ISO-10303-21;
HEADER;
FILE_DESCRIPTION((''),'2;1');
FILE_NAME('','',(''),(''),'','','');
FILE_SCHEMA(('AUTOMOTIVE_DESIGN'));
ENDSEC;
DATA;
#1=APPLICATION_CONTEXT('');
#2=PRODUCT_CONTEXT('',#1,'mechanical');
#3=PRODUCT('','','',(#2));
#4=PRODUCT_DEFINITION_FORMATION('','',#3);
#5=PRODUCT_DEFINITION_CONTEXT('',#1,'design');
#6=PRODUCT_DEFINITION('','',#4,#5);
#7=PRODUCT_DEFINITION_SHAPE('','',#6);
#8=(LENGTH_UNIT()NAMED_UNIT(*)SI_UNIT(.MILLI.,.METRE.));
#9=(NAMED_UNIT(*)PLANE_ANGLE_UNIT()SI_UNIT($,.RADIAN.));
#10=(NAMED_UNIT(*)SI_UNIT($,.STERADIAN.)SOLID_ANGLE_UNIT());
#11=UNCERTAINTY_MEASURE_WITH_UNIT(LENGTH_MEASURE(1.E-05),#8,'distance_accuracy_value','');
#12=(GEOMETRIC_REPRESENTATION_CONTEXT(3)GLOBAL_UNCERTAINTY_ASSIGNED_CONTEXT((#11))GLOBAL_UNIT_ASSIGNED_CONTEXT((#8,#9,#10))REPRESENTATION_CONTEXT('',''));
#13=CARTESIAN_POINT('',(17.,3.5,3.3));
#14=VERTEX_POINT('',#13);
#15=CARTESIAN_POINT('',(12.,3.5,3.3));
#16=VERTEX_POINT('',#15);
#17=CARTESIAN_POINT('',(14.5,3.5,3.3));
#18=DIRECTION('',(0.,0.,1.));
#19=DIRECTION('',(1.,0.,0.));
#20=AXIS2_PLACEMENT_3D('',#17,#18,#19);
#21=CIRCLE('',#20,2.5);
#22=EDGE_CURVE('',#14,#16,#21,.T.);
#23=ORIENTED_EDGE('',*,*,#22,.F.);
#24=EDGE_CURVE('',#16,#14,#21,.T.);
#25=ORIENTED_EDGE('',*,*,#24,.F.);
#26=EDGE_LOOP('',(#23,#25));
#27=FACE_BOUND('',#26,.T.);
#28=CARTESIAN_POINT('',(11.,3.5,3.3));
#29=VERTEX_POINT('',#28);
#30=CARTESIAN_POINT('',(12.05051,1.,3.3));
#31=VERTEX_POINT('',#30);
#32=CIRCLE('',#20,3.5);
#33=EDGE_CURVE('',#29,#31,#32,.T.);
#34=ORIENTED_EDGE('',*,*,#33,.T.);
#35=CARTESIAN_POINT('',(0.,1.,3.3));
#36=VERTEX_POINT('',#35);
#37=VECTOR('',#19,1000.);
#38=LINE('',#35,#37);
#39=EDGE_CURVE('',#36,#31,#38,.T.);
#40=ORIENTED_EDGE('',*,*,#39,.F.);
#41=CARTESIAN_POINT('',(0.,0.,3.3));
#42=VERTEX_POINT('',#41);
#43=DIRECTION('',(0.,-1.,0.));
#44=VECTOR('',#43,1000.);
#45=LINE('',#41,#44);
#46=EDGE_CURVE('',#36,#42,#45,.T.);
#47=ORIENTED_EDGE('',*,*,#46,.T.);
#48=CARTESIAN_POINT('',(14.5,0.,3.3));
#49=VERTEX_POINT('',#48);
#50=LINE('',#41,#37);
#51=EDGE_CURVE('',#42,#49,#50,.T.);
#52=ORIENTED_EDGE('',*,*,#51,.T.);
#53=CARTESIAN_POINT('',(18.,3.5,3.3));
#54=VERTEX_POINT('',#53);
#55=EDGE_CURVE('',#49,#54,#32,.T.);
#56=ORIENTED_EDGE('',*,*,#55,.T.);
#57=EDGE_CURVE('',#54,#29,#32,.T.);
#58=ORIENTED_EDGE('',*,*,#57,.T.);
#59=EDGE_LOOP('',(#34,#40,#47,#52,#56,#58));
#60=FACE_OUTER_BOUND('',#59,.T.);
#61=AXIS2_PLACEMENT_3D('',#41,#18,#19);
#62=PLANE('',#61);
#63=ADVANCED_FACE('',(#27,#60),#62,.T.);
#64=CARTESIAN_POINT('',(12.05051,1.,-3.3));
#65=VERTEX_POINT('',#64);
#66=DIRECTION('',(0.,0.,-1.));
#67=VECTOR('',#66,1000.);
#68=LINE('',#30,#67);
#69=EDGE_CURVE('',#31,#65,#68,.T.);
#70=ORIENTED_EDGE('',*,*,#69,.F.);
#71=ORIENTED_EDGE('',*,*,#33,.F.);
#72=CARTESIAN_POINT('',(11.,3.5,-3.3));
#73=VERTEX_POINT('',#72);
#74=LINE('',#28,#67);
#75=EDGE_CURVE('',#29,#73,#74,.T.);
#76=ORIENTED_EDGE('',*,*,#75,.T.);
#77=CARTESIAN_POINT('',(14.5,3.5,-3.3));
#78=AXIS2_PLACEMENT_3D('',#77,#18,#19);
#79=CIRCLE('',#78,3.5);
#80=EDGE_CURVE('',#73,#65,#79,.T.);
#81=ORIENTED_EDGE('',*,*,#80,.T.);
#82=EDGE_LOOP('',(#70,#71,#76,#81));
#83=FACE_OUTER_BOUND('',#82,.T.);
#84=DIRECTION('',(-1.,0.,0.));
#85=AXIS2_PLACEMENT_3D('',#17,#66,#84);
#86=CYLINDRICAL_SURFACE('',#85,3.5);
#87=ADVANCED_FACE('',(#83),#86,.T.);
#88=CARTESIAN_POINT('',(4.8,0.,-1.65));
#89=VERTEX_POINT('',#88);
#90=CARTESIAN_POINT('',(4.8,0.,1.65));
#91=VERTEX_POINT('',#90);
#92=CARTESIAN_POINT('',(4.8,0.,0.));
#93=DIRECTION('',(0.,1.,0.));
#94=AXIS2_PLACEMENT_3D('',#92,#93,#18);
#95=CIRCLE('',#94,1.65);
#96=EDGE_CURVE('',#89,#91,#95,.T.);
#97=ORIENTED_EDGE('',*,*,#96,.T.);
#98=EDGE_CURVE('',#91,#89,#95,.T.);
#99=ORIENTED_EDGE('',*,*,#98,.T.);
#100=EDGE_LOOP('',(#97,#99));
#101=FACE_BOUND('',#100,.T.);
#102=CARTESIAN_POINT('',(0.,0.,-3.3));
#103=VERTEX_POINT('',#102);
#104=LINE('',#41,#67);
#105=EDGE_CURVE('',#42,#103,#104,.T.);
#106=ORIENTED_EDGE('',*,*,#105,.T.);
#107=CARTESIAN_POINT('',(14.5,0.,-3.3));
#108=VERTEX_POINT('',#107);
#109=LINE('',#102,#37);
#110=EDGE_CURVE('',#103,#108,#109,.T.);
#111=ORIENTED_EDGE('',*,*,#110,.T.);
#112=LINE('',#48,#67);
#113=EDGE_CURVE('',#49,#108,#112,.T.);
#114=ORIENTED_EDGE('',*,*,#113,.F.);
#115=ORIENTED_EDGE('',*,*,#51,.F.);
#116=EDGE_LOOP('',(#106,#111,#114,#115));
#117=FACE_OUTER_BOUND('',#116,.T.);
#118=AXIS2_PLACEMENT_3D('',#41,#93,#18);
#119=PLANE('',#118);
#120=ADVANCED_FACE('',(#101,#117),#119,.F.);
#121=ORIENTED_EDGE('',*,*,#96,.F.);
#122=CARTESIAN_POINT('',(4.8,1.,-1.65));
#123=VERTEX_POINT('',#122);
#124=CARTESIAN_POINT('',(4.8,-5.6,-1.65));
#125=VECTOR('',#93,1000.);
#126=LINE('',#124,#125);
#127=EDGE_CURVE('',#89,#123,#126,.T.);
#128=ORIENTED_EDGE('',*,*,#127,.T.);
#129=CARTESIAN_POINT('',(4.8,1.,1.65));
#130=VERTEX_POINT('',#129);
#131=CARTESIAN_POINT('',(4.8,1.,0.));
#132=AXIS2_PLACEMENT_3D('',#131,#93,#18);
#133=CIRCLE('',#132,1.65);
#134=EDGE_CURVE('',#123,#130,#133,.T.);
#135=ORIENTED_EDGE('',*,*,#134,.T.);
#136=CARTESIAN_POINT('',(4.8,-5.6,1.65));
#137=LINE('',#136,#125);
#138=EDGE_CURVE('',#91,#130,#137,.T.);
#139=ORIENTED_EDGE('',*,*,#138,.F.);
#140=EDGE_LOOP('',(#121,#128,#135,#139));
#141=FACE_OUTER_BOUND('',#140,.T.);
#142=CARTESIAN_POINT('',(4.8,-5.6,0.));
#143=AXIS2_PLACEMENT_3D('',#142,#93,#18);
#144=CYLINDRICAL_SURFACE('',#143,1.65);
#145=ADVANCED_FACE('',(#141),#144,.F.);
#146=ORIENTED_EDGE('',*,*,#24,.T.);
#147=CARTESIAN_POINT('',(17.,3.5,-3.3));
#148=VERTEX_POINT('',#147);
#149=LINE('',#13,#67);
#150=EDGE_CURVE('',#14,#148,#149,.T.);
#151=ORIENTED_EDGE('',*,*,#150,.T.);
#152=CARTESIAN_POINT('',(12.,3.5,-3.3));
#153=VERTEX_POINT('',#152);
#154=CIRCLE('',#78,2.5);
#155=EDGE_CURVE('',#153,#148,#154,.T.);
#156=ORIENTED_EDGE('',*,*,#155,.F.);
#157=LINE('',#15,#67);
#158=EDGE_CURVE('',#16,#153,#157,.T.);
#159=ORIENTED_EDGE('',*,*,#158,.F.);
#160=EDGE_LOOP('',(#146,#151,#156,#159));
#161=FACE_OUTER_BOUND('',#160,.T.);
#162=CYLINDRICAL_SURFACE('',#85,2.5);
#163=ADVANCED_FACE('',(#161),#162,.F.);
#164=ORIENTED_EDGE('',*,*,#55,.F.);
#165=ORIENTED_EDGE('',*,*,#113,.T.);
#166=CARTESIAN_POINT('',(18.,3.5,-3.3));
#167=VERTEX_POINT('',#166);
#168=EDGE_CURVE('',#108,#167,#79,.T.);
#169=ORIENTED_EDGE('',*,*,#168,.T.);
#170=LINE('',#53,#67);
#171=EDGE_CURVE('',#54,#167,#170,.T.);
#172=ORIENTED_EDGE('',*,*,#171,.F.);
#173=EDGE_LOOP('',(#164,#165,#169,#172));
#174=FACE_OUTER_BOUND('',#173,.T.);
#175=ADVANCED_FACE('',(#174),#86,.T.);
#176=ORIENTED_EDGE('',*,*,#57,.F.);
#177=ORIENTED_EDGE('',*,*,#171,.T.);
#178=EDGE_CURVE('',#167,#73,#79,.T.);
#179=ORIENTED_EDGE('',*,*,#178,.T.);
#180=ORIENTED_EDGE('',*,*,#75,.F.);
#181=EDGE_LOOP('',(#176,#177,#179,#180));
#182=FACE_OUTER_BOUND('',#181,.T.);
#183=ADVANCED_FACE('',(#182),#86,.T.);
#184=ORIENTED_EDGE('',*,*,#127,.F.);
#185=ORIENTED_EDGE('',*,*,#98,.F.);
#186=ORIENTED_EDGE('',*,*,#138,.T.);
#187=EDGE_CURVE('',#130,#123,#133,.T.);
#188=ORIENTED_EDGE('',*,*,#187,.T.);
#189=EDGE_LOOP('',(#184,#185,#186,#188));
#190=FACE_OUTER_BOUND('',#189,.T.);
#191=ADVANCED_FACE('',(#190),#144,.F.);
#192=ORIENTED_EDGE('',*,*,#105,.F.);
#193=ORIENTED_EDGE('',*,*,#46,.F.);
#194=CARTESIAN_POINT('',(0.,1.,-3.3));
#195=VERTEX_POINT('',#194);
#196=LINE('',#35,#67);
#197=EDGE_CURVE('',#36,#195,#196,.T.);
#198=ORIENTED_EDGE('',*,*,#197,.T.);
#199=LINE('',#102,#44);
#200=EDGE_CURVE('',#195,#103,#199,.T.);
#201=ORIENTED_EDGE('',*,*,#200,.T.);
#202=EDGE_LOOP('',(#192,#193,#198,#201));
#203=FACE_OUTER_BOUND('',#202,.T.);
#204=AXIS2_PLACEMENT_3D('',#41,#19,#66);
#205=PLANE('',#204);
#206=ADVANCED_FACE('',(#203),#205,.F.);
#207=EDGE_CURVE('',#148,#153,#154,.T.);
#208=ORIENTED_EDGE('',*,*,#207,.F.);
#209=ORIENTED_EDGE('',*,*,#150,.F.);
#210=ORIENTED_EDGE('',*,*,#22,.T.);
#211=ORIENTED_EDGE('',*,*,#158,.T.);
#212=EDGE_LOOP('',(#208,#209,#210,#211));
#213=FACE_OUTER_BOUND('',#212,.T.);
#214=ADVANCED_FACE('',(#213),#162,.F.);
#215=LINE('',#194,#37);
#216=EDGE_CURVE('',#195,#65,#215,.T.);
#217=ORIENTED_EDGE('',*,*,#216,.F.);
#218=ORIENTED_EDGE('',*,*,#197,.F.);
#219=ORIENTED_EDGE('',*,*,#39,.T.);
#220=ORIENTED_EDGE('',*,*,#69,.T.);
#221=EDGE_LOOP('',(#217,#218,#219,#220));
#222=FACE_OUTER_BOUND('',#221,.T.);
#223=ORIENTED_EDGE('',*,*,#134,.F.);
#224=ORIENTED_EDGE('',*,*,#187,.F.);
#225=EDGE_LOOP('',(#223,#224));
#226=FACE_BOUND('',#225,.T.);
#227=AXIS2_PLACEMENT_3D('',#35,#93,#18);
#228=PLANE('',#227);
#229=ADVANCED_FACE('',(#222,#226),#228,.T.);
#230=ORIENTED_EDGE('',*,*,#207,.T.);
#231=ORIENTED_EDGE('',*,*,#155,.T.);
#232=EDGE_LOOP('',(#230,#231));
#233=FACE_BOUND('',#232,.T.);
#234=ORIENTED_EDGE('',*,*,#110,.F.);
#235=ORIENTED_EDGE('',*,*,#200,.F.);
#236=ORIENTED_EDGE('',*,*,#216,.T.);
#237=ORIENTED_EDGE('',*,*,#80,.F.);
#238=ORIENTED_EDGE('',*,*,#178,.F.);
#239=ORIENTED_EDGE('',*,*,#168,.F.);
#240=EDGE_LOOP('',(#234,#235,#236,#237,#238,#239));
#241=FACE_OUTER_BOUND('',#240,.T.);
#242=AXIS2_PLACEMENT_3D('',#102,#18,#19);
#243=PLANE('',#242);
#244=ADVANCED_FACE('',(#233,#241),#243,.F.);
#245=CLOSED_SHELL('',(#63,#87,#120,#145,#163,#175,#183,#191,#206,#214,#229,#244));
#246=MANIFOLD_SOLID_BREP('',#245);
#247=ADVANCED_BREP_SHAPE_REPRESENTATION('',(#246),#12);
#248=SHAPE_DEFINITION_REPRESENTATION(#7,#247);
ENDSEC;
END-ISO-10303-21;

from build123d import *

# Parameters (mm, degrees)
SKETCH_1_R          = 2.5
EXTRUDE_1_DEPTH     = 3.3
SKETCH_2_R          = 1.65
CUT_EXTRUDE_1_DEPTH = 6.6


with BuildPart() as part:
    # 草图1 → 凸台-拉伸1 (new, symmetric)
    with BuildSketch(Plane.XY):
        with BuildLine():
            Line((0, 1), (0, 0))
            Line((0, 0), (14.5, 0))
            ThreePointArc((14.5, 0), (15.822875656, 6.740370349), (12.050510257, 1))
            Line((12.050510257, 1), (0, 1))
        make_face()
        with Locations((14.5, 3.5)):
            Circle(SKETCH_1_R, mode=Mode.SUBTRACT)
    extrude(amount=EXTRUDE_1_DEPTH, both=True)

    # 草图2 → 切除-拉伸1 (cut)
    with BuildSketch(Plane(origin=(0, 1, 0), x_dir=(1, 0, 0), z_dir=(0, 1, 0))):
        with Locations(Location((4.8, 0, 0), (0, 0, 270))):
            Circle(SKETCH_2_R)
    extrude(amount=-CUT_EXTRUDE_1_DEPTH, mode=Mode.SUBTRACT)


solid = part.part
